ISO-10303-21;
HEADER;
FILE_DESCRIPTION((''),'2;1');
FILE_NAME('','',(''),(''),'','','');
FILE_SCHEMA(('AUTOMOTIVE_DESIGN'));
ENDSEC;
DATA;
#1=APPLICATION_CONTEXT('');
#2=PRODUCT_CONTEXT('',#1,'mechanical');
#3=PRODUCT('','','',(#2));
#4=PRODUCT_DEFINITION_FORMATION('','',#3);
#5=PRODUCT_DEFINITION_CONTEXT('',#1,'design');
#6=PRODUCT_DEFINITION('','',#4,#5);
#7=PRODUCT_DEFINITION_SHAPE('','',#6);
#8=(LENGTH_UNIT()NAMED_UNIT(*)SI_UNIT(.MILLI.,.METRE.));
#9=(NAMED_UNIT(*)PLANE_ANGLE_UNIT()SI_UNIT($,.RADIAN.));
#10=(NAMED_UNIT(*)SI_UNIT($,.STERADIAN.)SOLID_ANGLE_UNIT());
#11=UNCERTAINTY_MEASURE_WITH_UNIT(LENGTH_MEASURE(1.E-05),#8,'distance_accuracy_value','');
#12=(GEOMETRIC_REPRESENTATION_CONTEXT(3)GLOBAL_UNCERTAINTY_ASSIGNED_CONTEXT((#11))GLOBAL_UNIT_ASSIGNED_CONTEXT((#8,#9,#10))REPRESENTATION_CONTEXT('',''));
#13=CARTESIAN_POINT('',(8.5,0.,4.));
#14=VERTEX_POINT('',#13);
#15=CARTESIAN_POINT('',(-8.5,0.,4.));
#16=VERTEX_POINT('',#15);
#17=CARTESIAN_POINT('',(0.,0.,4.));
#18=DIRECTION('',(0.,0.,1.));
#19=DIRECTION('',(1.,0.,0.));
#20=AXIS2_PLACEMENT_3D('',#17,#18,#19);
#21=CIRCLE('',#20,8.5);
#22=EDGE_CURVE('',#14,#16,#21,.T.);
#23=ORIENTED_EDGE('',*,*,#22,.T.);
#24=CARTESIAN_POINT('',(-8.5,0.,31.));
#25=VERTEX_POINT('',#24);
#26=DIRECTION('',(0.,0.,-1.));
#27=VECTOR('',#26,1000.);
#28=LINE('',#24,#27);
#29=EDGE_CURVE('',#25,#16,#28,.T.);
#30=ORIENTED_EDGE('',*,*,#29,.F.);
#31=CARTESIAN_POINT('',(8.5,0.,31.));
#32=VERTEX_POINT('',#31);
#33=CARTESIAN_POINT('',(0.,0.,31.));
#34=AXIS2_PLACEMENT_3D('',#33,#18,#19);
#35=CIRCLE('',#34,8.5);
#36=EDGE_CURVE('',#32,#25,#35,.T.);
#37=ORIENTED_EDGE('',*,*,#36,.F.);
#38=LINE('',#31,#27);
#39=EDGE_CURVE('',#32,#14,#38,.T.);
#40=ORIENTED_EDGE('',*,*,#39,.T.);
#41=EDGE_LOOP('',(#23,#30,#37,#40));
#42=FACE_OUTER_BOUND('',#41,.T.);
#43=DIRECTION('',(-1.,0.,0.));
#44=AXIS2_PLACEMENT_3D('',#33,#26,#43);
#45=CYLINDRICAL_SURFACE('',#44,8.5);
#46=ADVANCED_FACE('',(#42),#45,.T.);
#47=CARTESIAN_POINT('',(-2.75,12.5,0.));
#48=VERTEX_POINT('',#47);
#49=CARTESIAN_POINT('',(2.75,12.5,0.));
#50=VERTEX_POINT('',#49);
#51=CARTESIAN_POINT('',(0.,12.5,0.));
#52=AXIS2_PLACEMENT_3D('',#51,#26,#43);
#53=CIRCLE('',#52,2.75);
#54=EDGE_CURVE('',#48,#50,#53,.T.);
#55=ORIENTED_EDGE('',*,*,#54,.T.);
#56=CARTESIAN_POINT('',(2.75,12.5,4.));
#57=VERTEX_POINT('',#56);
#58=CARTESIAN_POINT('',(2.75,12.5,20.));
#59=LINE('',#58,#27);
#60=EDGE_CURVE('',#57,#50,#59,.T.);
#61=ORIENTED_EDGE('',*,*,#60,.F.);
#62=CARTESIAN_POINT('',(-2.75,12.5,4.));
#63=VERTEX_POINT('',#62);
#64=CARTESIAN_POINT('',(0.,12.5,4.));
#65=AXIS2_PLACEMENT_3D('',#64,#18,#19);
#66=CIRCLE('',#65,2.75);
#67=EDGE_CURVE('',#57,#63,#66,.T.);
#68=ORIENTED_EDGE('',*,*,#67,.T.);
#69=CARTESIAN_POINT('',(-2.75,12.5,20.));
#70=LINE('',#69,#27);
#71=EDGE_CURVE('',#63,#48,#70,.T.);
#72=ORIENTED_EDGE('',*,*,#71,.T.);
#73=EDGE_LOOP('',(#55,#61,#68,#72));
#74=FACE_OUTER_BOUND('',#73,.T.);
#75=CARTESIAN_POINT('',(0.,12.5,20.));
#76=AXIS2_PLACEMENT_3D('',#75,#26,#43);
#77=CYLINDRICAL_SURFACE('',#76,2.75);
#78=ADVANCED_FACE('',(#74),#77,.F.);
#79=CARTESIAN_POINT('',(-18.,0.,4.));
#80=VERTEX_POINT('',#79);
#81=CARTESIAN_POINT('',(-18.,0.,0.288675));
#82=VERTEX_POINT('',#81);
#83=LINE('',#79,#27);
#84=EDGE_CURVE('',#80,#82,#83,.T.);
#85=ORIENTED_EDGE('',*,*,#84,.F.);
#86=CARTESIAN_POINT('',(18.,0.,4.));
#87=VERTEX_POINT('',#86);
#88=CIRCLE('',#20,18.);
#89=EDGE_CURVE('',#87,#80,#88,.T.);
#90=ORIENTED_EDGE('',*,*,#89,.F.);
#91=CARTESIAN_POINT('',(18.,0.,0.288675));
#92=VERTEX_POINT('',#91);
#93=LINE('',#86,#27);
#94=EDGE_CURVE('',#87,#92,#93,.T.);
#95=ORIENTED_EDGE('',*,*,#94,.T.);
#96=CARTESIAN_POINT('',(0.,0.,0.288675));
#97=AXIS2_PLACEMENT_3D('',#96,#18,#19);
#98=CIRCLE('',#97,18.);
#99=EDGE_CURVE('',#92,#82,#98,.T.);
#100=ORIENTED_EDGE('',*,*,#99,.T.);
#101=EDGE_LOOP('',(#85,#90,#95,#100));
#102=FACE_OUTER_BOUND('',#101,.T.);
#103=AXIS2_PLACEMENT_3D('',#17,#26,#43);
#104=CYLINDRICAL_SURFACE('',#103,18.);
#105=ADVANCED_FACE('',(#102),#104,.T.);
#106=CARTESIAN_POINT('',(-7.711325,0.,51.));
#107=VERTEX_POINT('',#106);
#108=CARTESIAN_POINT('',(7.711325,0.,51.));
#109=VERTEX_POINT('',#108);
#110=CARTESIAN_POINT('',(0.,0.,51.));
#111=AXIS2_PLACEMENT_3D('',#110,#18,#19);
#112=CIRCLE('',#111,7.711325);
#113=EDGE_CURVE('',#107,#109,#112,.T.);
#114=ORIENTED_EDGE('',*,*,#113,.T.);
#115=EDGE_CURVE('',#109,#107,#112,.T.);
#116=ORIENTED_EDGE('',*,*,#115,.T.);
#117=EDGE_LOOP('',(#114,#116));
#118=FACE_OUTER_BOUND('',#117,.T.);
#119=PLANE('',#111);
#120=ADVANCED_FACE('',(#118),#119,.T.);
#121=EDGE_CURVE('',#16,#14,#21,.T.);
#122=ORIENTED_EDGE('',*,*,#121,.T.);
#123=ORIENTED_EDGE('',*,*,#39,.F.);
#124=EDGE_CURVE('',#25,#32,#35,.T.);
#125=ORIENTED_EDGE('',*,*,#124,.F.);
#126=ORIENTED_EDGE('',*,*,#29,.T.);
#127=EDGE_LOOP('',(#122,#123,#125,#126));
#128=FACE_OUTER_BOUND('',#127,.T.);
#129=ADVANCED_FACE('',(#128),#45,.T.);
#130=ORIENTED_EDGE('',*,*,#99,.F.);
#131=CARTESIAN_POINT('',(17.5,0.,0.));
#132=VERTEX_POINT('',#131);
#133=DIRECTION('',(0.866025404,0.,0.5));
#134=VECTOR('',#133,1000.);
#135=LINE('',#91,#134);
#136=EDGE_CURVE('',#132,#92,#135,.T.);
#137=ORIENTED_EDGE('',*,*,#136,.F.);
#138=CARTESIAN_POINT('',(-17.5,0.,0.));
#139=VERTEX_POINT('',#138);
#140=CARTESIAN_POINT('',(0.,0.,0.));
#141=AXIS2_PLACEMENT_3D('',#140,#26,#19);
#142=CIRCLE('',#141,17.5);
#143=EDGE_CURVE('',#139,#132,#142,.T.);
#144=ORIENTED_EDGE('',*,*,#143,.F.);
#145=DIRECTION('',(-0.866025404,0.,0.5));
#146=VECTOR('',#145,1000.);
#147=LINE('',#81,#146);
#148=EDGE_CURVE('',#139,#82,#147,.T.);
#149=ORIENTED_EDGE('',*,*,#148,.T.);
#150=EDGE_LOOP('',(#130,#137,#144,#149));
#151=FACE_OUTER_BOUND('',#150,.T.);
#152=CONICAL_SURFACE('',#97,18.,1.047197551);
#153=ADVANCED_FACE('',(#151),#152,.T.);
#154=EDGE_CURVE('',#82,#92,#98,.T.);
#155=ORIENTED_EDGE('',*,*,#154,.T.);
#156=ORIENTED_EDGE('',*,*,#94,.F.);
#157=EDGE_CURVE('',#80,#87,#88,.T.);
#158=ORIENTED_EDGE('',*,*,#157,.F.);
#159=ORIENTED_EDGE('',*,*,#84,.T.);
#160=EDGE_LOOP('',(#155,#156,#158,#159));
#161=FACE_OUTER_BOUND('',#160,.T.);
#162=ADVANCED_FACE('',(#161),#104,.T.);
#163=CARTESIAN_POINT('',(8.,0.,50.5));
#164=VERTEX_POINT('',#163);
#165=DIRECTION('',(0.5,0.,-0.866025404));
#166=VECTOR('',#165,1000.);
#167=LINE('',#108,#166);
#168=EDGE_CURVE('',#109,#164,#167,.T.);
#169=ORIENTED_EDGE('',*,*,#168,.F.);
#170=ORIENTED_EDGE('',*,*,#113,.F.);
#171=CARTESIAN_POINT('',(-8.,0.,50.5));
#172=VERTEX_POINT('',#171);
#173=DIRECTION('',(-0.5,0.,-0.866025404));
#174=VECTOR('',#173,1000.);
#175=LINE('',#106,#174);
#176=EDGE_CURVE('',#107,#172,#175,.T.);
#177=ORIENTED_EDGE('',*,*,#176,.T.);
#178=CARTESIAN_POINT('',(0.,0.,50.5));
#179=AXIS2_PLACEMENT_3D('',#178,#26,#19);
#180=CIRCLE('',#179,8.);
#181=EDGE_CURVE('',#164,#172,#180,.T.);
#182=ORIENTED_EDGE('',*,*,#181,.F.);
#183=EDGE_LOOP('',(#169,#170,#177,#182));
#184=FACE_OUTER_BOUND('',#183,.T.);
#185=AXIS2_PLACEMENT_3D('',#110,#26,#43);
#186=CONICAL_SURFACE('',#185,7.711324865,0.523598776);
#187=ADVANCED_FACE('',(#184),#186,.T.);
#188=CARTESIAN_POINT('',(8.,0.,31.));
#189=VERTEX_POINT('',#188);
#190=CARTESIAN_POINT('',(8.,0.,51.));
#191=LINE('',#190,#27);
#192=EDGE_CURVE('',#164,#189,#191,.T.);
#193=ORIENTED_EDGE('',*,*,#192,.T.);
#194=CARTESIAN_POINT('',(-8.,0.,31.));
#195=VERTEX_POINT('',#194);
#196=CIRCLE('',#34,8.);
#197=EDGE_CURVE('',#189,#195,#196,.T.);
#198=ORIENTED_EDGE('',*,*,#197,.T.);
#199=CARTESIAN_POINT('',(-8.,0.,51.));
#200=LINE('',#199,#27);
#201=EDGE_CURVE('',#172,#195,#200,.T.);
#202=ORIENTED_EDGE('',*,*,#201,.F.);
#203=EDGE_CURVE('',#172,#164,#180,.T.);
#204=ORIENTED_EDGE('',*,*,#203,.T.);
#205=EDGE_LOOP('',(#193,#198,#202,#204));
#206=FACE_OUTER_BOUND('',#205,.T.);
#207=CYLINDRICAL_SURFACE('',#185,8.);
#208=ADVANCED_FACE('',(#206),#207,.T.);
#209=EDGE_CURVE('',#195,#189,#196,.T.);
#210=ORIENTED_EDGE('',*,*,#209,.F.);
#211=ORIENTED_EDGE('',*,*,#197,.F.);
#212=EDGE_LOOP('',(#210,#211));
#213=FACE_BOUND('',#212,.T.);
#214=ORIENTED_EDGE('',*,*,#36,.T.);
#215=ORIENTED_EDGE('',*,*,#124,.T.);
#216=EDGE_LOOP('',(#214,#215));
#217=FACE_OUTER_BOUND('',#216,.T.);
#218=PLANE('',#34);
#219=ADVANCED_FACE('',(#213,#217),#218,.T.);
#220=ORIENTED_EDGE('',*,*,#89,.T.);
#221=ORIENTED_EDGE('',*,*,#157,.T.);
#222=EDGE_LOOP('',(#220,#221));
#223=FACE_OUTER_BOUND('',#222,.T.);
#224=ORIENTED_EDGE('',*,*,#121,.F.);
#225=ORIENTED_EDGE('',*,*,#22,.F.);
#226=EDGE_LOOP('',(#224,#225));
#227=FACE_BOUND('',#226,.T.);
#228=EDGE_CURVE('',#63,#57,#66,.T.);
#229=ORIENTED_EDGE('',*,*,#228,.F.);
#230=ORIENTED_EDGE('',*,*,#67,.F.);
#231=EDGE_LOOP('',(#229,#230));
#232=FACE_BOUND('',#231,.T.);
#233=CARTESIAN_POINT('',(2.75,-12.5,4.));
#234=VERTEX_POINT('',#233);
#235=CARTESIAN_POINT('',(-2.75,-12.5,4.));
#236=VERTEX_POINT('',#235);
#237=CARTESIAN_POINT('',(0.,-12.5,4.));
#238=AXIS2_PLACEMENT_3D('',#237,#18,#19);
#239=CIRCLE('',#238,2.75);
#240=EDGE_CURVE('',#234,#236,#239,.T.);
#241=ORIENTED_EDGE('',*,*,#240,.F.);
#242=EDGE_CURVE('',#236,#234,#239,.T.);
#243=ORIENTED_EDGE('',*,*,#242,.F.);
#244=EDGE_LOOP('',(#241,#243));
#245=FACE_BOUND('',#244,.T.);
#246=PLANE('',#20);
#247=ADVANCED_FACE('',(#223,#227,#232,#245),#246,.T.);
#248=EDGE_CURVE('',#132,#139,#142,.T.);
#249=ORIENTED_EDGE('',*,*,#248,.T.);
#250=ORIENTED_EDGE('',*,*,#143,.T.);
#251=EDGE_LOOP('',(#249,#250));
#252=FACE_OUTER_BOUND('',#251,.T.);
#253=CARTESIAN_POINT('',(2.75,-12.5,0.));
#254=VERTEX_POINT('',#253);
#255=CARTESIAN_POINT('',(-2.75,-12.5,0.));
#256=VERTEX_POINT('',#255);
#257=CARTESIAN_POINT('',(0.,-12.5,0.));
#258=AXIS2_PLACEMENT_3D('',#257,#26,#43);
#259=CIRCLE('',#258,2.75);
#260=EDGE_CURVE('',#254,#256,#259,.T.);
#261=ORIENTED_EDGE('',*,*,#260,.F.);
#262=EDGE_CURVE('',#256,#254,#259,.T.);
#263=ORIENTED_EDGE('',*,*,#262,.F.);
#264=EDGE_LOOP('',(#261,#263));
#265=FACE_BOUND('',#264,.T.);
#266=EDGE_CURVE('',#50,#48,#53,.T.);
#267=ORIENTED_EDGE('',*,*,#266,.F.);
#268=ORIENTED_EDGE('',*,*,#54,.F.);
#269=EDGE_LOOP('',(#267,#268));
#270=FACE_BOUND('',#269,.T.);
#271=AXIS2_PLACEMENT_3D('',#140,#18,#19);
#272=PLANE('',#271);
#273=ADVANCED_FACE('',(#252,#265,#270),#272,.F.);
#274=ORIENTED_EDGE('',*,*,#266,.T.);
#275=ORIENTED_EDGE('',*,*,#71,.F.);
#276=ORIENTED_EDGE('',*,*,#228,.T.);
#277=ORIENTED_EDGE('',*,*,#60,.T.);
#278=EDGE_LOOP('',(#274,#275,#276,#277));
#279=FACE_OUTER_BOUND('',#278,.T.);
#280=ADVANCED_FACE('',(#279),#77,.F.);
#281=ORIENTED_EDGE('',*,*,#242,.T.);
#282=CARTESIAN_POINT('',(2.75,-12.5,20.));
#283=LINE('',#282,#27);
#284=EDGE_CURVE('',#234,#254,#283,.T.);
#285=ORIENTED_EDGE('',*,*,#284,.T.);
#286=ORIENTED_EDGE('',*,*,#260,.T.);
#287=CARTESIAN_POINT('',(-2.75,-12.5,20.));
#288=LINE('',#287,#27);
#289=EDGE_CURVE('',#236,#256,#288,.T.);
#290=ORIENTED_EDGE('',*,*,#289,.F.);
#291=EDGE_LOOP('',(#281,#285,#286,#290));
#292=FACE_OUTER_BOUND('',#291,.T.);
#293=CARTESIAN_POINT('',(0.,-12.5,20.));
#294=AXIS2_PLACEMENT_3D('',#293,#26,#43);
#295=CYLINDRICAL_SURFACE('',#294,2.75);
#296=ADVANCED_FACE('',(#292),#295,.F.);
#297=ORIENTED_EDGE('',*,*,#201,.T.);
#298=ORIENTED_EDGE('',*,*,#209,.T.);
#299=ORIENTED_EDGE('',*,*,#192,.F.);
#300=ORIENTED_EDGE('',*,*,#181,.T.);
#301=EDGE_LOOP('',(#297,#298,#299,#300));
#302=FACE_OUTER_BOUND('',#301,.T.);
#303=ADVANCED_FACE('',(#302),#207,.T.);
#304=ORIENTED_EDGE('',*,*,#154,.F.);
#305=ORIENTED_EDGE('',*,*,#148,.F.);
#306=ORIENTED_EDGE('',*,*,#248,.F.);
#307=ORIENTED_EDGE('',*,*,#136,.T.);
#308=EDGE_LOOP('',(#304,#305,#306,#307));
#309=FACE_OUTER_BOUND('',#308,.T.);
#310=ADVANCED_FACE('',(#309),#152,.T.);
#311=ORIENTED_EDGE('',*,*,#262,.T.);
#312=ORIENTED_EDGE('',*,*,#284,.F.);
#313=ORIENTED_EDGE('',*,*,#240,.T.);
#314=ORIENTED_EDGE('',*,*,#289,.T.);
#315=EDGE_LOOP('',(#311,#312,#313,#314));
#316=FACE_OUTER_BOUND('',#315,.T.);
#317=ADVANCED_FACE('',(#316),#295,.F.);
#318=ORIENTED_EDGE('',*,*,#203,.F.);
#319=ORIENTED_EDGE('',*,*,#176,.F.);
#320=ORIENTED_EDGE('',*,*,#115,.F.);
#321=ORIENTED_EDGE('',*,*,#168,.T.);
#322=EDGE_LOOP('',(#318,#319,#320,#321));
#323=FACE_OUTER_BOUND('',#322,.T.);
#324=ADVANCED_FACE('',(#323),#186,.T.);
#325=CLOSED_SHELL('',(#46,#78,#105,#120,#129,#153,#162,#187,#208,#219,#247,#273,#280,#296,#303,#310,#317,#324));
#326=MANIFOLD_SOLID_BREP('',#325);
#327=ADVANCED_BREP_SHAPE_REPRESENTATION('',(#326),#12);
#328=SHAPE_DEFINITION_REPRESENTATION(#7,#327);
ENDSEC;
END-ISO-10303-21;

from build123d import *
from OCP.BRepFilletAPI import BRepFilletAPI_MakeChamfer

# Parameters (mm, degrees)
SKETCH1_R           = 18
BOSS_EXTRUDE1_DEPTH = 4
SKETCH2_R           = 8.5
BOSS_EXTRUDE2_DEPTH = 27
BOSS_EXTRUDE3_START = 27
SKETCH3_R           = 8
BOSS_EXTRUDE3_DEPTH = 20
CHAMFER1_SIZE       = 0.5
CHAMFER1_SIZE2      = 0.288675135
SKETCH4_R           = 2.75
CUT_EXTRUDE1_DEPTH  = 20


with BuildPart() as part:
    # Sketch1 → Boss-Extrude1 (new body)
    with BuildSketch(Plane.XY):
        Circle(SKETCH1_R)
    extrude(amount=BOSS_EXTRUDE1_DEPTH)

    # Sketch2 → Boss-Extrude2 (add)
    with BuildSketch(Plane.XY.offset(4)):
        Circle(SKETCH2_R)
    extrude(amount=BOSS_EXTRUDE2_DEPTH)

    # Sketch3 → Boss-Extrude3 (add)
    with BuildSketch(Plane.XY.offset(4).offset(BOSS_EXTRUDE3_START)):
        Circle(SKETCH3_R)
    extrude(amount=BOSS_EXTRUDE3_DEPTH)

    # Chamfer1: one chamfer whose edges measure the first distance from different faces: ONE call of the kernel's chamfer builder (chamfer() names one face for all edges)
    chamfer1_edges_1 = [part.edges().sort_by_distance(p)[0] for p in [
        (-8, 0, 51),
    ]]
    chamfer1_side_1 = [part.faces().sort_by_distance(p)[0] for p in [
        (-8, 0, 41),
    ]]
    chamfer1_edges_2 = [part.edges().sort_by_distance(p)[0] for p in [
        (-18, 0, 0),
    ]]
    chamfer1_side_2 = [part.faces().sort_by_distance(p)[0] for p in [
        (0, 0, 0),
    ]]
    chamfer1 = BRepFilletAPI_MakeChamfer(part.part.solid().wrapped)
    for e in chamfer1_edges_1:
        chamfer1.Add(CHAMFER1_SIZE, CHAMFER1_SIZE2, e.wrapped, chamfer1_side_1[0].wrapped)  # the first distance lies on this face
    for e in chamfer1_edges_2:
        chamfer1.Add(CHAMFER1_SIZE, CHAMFER1_SIZE2, e.wrapped, chamfer1_side_2[0].wrapped)  # the first distance lies on this face
    add(Compound.cast(chamfer1.Shape()), mode=Mode.REPLACE)

    # Sketch4 → Cut-Extrude1 (cut)
    with BuildSketch(Plane(origin=(0, 0, 0), x_dir=(-1, 0, 0), z_dir=(0, 0, -1))):
        with Locations((0, 12.5)):
            Circle(SKETCH4_R)
        with Locations((0, -12.5)):
            Circle(SKETCH4_R)
    extrude(amount=-CUT_EXTRUDE1_DEPTH, mode=Mode.SUBTRACT)


solid = part.part
